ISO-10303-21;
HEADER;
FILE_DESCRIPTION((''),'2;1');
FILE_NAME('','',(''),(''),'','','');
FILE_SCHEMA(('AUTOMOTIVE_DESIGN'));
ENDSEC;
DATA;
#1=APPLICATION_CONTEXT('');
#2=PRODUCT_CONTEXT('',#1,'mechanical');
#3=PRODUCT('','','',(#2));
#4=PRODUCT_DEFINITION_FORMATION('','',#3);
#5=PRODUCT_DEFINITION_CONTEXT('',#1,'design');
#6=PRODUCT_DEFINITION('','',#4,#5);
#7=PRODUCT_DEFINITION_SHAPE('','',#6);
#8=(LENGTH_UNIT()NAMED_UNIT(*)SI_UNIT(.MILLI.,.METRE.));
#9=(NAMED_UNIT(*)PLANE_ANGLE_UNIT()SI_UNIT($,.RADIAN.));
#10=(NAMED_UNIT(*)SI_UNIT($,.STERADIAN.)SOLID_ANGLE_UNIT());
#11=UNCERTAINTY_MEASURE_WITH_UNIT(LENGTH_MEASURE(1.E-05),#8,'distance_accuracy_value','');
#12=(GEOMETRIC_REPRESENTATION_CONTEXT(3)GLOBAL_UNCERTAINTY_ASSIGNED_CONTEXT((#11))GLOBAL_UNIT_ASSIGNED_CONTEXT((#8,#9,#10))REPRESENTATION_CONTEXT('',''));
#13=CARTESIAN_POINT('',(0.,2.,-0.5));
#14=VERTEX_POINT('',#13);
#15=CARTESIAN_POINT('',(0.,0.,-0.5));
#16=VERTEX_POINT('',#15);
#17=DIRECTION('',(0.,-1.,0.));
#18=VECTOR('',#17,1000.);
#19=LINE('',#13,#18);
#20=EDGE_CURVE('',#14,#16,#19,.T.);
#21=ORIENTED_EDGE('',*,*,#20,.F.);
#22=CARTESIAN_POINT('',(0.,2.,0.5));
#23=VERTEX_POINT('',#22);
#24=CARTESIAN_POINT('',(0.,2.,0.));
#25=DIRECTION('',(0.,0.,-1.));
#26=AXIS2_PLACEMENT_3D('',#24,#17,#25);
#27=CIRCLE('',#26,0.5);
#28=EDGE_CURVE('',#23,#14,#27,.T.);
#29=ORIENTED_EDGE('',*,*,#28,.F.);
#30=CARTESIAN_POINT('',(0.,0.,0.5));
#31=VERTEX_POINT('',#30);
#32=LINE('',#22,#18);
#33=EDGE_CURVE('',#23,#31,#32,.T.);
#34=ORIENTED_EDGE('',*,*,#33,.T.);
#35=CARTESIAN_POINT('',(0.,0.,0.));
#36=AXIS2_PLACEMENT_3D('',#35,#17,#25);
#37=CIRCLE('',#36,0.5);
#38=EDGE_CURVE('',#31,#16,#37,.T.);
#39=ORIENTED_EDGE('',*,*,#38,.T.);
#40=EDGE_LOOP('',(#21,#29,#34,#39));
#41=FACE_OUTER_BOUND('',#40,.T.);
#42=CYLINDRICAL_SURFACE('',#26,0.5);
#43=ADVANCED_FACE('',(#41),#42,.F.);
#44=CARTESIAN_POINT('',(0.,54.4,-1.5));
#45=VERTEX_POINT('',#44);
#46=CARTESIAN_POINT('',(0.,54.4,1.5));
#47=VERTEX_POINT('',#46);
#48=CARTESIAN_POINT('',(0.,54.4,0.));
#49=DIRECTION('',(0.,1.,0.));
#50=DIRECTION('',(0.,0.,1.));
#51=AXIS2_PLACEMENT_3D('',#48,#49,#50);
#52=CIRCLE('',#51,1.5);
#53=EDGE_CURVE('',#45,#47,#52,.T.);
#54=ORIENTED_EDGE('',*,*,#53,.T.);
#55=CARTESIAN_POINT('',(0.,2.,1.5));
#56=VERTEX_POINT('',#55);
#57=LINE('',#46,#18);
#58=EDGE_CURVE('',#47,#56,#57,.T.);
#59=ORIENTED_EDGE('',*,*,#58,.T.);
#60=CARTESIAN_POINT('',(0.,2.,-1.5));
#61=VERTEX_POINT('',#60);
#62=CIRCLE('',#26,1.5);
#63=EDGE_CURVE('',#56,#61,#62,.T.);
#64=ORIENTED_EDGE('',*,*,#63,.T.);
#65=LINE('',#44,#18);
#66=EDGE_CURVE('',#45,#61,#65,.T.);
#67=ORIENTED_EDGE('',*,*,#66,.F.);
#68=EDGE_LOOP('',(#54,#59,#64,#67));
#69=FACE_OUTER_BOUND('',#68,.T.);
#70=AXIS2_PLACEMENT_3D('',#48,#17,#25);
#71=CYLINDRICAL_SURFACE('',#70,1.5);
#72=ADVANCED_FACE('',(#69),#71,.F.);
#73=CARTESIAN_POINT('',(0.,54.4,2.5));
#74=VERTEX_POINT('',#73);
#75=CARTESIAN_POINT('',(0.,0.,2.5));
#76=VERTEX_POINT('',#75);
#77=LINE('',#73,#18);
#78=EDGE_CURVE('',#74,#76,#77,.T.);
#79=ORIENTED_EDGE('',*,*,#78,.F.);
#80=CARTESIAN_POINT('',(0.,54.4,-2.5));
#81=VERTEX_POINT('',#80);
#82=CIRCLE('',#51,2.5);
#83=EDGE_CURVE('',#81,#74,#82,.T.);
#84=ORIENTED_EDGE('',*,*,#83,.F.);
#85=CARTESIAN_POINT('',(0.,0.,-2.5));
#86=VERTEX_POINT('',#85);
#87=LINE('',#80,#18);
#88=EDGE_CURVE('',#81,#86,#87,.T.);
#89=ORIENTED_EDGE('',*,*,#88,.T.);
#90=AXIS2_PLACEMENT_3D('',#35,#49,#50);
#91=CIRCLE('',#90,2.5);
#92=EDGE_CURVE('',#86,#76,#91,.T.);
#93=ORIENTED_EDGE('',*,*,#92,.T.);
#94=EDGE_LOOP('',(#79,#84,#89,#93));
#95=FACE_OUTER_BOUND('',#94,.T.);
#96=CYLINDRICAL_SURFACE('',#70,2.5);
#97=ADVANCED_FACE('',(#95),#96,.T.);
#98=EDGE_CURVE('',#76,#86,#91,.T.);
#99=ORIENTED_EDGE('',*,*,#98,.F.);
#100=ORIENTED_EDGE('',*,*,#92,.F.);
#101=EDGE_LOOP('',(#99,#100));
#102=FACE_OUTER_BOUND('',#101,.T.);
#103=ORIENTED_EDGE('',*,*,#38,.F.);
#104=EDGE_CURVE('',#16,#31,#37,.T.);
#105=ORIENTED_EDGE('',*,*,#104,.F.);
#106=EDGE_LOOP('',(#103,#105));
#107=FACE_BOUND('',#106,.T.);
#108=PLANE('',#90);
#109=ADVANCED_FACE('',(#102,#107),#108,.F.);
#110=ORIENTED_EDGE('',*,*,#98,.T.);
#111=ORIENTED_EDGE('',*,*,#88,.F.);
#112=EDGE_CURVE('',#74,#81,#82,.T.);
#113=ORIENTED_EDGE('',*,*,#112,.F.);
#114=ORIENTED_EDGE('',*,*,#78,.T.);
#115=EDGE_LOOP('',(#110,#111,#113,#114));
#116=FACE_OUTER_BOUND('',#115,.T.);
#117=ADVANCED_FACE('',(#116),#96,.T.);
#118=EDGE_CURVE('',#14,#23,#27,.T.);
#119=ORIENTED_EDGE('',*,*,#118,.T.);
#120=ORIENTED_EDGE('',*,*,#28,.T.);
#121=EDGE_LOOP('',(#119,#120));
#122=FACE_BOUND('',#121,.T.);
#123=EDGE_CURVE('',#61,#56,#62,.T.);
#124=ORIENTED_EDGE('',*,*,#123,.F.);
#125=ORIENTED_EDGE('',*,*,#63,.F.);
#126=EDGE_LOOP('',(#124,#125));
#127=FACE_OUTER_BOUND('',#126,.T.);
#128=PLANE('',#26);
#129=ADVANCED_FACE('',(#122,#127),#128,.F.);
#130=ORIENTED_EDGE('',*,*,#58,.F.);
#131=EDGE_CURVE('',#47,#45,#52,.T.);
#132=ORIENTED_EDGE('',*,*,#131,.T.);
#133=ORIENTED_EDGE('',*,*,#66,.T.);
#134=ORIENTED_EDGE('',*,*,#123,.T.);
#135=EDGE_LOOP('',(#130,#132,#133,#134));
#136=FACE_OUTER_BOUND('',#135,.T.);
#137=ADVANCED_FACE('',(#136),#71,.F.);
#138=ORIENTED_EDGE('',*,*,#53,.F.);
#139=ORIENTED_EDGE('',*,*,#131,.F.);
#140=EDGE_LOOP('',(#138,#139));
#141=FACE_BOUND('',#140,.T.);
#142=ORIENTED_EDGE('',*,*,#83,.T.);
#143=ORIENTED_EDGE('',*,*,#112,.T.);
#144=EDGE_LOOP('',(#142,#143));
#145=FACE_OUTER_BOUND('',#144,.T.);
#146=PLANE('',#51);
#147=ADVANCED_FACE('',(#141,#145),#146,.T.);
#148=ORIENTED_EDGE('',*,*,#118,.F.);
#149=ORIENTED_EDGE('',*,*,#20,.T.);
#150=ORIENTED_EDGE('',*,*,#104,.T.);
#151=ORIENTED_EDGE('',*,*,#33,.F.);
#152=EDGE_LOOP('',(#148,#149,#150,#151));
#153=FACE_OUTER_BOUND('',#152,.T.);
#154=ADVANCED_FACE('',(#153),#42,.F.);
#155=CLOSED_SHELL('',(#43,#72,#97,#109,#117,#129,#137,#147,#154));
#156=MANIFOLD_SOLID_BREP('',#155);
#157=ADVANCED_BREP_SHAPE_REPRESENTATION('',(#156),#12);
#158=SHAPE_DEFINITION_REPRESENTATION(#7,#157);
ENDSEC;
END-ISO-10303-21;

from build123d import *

# Parameters (mm, degrees)
SKETCH1_R           = 2.5
SKETCH1_R_2         = 1.5
BOSS_EXTRUDE1_DEPTH = 54.4
SKETCH2_R           = 1.5
SKETCH2_R_2         = 0.5
BOSS_EXTRUDE2_DEPTH = 2


with BuildPart() as part:
    # Sketch1 → Boss-Extrude1 (new body)
    with BuildSketch(Plane(origin=(0, 0, 0), x_dir=(1, 0, 0), z_dir=(0, 1, 0))):
        with Locations(Location((0, 0, 0), (0, 0, 270))):
            Circle(SKETCH1_R)
        with Locations(Location((0, 0, 0), (0, 0, 270))):
            Circle(SKETCH1_R_2, mode=Mode.SUBTRACT)
    extrude(amount=BOSS_EXTRUDE1_DEPTH)

    # Sketch2 → Boss-Extrude2 (add)
    with BuildSketch(Plane.XZ):
        with Locations(Location((0, 0, 0), (0, 0, 270))):
            Circle(SKETCH2_R)
        with Locations(Location((0, 0, 0), (0, 0, 270))):
            Circle(SKETCH2_R_2, mode=Mode.SUBTRACT)
    extrude(amount=-BOSS_EXTRUDE2_DEPTH)


solid = part.part
